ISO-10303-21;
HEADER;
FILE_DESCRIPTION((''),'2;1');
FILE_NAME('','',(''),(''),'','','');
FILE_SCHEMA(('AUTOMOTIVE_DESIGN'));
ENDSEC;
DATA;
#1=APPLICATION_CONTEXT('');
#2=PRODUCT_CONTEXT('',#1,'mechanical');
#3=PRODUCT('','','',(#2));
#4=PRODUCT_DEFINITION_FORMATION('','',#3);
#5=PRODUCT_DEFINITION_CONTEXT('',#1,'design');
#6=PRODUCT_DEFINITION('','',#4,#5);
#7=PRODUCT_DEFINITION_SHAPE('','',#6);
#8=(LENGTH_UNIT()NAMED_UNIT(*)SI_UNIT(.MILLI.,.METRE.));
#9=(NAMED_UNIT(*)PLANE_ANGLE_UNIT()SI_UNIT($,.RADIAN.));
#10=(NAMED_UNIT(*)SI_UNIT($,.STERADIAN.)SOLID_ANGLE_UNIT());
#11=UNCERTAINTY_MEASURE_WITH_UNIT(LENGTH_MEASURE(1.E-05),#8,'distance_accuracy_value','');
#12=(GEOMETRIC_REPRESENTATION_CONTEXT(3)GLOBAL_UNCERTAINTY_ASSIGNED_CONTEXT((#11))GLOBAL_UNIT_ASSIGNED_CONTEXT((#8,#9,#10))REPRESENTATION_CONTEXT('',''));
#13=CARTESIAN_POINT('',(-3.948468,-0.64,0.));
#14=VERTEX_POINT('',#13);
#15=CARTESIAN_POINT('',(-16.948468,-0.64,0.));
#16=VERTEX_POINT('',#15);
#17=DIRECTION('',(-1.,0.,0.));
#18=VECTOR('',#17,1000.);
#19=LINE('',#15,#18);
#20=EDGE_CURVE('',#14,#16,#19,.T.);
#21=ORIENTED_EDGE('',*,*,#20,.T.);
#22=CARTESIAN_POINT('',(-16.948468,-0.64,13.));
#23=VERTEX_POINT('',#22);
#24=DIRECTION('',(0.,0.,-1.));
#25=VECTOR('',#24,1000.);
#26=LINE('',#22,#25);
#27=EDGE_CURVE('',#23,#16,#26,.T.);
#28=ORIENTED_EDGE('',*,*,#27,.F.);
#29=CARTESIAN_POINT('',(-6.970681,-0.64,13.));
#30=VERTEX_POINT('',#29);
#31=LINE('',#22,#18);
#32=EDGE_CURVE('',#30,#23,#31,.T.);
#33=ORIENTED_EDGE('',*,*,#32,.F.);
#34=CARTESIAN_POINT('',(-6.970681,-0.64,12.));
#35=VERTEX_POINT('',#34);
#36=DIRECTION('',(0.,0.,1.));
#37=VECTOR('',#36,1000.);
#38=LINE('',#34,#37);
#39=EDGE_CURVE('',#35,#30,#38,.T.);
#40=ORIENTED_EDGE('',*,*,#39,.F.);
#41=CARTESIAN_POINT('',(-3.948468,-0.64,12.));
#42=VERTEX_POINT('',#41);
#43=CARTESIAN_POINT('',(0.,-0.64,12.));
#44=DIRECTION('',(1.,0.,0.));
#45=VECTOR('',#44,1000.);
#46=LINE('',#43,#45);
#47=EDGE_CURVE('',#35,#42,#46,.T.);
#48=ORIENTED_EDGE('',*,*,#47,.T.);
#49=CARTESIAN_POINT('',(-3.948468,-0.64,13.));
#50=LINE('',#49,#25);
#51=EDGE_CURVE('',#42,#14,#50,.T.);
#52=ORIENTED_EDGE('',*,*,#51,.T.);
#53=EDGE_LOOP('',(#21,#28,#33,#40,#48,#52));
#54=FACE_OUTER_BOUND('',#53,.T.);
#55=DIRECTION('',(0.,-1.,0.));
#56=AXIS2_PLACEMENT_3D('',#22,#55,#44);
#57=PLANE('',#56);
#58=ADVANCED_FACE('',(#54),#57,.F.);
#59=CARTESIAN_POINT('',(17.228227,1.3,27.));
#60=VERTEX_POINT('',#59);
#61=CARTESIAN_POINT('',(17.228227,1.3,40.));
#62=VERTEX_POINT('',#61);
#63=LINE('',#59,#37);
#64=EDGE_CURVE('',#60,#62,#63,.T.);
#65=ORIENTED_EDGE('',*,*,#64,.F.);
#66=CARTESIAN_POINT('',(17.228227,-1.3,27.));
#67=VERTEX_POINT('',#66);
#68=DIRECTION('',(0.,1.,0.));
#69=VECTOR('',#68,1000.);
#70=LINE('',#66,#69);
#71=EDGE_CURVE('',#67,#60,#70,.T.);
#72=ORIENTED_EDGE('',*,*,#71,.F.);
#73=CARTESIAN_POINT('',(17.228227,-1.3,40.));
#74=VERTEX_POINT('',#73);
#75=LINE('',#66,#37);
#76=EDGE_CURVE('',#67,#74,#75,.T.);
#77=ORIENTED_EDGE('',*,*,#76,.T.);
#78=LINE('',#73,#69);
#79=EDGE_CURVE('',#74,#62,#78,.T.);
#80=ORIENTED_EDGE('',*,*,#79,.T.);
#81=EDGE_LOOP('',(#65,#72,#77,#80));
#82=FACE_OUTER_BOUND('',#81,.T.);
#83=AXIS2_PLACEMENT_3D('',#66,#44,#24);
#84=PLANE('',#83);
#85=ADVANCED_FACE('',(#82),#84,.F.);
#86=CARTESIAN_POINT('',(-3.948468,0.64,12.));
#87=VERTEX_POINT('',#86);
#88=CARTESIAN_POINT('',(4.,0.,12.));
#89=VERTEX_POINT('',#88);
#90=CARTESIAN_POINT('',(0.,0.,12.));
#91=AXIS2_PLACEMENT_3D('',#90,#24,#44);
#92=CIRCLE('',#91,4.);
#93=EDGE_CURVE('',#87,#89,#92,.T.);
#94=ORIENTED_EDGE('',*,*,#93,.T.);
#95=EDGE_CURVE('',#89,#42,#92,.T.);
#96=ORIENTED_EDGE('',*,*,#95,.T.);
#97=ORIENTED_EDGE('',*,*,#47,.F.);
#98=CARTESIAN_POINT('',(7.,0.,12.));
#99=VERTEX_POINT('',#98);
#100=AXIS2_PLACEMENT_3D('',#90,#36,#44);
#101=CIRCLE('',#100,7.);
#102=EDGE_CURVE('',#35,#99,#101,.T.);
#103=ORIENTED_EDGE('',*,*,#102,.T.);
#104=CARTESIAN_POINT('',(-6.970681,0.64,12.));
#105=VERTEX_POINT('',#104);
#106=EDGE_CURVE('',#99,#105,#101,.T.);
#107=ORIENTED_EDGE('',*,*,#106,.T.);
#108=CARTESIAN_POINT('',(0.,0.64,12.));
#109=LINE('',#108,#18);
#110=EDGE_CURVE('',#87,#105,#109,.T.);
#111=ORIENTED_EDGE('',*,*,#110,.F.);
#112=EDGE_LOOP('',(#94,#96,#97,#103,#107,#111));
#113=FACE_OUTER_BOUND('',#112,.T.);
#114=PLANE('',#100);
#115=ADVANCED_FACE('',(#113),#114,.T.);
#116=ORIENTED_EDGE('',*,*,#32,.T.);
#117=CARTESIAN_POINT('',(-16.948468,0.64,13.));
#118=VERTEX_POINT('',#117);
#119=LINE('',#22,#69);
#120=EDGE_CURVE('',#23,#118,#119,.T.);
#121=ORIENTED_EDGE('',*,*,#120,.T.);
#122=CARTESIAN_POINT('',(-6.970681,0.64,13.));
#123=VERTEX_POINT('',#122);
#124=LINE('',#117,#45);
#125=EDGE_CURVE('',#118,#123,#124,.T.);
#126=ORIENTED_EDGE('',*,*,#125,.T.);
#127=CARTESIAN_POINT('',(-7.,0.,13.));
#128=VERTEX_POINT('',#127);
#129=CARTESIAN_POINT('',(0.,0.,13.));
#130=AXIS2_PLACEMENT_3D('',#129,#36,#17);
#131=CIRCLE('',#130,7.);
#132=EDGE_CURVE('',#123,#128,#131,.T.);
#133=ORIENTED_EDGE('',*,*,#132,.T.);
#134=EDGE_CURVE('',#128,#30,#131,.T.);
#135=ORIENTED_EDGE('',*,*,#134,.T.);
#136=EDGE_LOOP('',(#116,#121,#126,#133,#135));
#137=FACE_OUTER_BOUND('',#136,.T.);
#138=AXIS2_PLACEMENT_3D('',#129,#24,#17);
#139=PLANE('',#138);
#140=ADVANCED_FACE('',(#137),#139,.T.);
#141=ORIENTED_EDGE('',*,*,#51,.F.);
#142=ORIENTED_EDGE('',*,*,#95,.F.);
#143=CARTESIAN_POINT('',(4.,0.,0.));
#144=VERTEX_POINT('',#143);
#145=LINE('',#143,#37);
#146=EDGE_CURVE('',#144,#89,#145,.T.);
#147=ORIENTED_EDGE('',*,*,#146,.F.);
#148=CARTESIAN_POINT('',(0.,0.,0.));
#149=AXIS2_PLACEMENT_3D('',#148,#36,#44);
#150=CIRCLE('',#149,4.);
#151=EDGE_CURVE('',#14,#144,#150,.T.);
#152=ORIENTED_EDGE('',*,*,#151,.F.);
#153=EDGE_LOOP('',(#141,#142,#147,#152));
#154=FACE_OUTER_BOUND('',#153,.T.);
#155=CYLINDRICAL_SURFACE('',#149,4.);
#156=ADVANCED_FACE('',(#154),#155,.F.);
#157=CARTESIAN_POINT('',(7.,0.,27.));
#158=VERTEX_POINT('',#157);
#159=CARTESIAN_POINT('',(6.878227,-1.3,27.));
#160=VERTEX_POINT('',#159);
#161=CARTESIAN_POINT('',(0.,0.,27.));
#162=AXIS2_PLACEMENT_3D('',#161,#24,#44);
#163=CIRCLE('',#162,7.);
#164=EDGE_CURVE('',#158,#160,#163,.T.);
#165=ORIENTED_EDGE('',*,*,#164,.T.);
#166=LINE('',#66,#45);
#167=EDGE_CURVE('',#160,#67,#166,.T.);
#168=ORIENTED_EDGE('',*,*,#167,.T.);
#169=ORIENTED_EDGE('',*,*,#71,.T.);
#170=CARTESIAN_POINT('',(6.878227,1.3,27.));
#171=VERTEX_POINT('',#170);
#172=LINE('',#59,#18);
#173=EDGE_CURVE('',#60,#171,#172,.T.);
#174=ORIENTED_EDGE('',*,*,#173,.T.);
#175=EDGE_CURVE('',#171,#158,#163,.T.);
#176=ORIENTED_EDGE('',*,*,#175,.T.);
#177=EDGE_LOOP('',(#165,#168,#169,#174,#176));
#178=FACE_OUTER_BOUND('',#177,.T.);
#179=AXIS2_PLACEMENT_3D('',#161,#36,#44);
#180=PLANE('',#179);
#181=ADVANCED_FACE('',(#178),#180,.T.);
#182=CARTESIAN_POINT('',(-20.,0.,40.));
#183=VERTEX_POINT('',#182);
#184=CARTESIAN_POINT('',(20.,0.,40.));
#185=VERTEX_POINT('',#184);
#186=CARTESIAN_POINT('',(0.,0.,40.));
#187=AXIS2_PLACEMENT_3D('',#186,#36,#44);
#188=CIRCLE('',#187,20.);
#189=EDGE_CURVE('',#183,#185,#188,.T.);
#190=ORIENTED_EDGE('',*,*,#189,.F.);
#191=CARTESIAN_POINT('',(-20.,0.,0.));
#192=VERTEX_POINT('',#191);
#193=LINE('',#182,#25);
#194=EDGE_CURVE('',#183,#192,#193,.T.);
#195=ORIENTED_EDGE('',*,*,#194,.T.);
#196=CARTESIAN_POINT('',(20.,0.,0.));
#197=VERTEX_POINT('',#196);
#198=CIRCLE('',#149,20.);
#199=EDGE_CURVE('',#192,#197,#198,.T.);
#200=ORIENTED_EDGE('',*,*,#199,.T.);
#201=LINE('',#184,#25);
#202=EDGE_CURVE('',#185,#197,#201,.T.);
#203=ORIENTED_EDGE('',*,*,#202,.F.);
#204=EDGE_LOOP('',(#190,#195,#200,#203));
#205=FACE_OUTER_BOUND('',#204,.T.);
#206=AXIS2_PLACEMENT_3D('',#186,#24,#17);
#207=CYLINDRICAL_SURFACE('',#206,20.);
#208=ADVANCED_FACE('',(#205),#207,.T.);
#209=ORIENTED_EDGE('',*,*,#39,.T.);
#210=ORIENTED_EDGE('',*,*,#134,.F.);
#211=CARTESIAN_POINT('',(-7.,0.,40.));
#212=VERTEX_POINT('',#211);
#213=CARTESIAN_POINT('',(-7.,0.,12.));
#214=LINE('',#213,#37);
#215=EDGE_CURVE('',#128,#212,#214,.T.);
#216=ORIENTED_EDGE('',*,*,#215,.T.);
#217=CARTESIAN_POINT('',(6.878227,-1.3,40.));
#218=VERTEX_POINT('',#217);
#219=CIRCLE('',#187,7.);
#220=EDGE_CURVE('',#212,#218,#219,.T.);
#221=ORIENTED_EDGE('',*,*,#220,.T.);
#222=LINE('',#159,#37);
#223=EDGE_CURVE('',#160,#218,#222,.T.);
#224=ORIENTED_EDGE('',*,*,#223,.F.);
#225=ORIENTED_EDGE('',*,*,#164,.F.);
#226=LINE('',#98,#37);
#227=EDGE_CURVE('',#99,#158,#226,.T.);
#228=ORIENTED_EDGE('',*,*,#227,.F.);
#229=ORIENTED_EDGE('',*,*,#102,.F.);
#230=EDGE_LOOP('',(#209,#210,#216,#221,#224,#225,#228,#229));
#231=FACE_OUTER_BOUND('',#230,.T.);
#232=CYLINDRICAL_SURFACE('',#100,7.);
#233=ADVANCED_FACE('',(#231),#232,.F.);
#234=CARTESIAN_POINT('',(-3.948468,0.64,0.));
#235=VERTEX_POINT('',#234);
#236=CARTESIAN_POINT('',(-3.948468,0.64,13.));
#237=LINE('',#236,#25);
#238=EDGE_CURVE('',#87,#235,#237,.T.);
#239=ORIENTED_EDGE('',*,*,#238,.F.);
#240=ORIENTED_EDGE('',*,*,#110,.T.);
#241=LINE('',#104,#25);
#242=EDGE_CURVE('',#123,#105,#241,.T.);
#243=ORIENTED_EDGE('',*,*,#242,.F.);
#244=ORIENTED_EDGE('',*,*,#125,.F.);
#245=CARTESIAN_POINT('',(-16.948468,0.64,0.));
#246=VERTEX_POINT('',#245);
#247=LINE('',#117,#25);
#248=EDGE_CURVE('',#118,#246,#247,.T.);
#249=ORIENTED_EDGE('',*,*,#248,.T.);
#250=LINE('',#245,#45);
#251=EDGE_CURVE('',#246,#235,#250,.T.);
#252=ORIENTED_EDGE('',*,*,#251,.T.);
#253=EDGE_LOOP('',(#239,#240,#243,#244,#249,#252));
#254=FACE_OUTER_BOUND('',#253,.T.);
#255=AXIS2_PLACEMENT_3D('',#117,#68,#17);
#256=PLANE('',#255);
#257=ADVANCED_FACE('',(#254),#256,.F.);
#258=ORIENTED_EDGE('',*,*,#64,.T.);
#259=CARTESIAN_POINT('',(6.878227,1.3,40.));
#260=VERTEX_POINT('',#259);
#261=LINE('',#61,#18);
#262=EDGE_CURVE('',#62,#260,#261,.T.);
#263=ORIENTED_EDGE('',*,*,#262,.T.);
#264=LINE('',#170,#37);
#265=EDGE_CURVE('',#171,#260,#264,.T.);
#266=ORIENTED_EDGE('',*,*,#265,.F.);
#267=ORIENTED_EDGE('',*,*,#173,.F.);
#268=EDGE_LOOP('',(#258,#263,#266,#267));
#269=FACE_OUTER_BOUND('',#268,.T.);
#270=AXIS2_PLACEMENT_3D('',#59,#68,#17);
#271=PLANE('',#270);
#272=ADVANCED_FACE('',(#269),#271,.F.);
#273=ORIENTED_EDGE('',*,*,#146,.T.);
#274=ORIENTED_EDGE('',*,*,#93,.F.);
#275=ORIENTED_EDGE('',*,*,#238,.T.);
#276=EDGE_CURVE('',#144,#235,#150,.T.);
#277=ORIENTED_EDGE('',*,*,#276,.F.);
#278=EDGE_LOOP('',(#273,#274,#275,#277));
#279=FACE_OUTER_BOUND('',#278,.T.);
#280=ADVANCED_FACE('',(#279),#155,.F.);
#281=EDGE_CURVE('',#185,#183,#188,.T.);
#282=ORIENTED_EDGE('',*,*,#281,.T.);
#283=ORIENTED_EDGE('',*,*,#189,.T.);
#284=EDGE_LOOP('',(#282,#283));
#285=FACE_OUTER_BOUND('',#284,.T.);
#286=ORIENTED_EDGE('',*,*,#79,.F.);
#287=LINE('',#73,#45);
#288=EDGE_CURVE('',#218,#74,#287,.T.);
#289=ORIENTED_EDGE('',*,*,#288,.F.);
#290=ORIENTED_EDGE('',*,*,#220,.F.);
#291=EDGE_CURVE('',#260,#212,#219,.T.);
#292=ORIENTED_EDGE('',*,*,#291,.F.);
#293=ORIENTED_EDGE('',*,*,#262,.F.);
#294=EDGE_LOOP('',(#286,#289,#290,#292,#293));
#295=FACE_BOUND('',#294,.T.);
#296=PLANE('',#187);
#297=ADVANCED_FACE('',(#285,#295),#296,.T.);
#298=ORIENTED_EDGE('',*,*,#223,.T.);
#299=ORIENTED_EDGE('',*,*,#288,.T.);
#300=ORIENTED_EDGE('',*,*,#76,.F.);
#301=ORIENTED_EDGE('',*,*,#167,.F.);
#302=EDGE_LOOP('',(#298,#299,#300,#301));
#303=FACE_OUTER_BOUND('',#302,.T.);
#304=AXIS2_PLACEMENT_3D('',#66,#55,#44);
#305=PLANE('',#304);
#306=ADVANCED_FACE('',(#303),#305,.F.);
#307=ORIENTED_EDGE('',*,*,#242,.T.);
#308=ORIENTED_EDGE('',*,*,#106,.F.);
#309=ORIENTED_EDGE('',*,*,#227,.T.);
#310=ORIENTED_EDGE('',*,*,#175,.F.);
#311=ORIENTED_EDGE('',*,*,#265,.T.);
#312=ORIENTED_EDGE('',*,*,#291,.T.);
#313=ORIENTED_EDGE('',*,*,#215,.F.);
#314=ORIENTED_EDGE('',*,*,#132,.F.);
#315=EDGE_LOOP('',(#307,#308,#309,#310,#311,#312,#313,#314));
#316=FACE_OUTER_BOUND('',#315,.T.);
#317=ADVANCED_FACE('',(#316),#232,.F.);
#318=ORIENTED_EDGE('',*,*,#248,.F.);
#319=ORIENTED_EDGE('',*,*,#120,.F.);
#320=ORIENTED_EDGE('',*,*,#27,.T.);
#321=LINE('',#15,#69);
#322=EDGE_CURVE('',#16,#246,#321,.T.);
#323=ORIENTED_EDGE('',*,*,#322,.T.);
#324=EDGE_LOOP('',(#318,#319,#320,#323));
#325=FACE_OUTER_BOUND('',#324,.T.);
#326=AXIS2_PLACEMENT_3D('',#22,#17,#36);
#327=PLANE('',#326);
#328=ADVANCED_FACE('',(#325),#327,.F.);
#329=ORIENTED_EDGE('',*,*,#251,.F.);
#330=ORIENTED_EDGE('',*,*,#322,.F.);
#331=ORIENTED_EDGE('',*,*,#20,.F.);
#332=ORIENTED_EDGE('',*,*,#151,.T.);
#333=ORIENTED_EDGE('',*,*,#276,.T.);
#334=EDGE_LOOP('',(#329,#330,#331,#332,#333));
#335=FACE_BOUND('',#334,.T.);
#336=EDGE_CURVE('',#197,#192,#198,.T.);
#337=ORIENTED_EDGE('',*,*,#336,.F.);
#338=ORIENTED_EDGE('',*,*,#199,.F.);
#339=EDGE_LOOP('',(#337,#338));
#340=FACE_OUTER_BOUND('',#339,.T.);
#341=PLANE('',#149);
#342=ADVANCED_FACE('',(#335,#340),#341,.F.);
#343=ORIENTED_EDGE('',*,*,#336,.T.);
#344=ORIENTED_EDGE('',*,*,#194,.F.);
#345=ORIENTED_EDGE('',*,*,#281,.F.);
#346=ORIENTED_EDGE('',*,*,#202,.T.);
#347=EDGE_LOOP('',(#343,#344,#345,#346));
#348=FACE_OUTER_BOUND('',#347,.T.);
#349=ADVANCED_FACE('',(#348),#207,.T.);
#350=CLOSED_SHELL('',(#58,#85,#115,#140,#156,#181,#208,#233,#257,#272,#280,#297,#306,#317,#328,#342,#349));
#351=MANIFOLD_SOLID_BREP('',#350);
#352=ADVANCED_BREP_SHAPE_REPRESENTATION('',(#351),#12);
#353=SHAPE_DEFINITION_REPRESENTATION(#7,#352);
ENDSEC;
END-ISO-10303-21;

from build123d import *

# Parameters (mm, degrees)
SKETCH_1_R          = 20
EXTRUDE_1_DEPTH     = 40
SKETCH_2_R          = 4
CUT_EXTRUDE_1_DEPTH = 49.989794856
SKETCH_3_R          = 7
CUT_EXTRUDE_2_DEPTH = 28
CUT_EXTRUDE_3_DEPTH = 13
CUT_EXTRUDE_START   = -13
CUT_EXTRUDE_4_DEPTH = 13


with BuildPart() as part:
    # 草图1 → 凸台-拉伸1 (new body)
    with BuildSketch(Plane.XY):
        Circle(SKETCH_1_R)
    extrude(amount=EXTRUDE_1_DEPTH)

    # 草图2 → 切除-拉伸1 (cut, through all)
    with BuildSketch(Plane.XY.offset(40)):
        Circle(SKETCH_2_R)
    extrude(amount=-CUT_EXTRUDE_1_DEPTH, mode=Mode.SUBTRACT)

    # 草图3 → 切除-拉伸2 (cut)
    with BuildSketch(Plane.XY.offset(40)):
        Circle(SKETCH_3_R)
    extrude(amount=-CUT_EXTRUDE_2_DEPTH, mode=Mode.SUBTRACT)

    # 草图4 → 切除-拉伸3 (cut)
    with BuildSketch(Plane.XY.offset(40)):
        with BuildLine():
            Line((17.228226516, -1.3), (17.228226516, 1.3))
            Line((17.228226516, 1.3), (6.878226516, 1.3))
            ThreePointArc((6.878226516, 1.3), (7, 0), (6.878226516, -1.3))
            Line((6.878226516, -1.3), (17.228226516, -1.3))
        make_face()
    extrude(amount=-CUT_EXTRUDE_3_DEPTH, mode=Mode.SUBTRACT)

    # 草图5 → 切除-拉伸4 (cut)
    with BuildSketch(Plane(origin=(0, 0, 0), x_dir=(-1, 0, 0), z_dir=(0, 0, -1)).offset(CUT_EXTRUDE_START)):
        with BuildLine():
            Line((16.948468057, -0.64), (16.948468057, 0.64))
            Line((16.948468057, 0.64), (3.948468057, 0.64))
            ThreePointArc((3.948468057, 0.64), (4, 0), (3.948468057, -0.64))
            Line((3.948468057, -0.64), (16.948468057, -0.64))
        make_face()
    extrude(amount=CUT_EXTRUDE_4_DEPTH, mode=Mode.SUBTRACT)


solid = part.part
